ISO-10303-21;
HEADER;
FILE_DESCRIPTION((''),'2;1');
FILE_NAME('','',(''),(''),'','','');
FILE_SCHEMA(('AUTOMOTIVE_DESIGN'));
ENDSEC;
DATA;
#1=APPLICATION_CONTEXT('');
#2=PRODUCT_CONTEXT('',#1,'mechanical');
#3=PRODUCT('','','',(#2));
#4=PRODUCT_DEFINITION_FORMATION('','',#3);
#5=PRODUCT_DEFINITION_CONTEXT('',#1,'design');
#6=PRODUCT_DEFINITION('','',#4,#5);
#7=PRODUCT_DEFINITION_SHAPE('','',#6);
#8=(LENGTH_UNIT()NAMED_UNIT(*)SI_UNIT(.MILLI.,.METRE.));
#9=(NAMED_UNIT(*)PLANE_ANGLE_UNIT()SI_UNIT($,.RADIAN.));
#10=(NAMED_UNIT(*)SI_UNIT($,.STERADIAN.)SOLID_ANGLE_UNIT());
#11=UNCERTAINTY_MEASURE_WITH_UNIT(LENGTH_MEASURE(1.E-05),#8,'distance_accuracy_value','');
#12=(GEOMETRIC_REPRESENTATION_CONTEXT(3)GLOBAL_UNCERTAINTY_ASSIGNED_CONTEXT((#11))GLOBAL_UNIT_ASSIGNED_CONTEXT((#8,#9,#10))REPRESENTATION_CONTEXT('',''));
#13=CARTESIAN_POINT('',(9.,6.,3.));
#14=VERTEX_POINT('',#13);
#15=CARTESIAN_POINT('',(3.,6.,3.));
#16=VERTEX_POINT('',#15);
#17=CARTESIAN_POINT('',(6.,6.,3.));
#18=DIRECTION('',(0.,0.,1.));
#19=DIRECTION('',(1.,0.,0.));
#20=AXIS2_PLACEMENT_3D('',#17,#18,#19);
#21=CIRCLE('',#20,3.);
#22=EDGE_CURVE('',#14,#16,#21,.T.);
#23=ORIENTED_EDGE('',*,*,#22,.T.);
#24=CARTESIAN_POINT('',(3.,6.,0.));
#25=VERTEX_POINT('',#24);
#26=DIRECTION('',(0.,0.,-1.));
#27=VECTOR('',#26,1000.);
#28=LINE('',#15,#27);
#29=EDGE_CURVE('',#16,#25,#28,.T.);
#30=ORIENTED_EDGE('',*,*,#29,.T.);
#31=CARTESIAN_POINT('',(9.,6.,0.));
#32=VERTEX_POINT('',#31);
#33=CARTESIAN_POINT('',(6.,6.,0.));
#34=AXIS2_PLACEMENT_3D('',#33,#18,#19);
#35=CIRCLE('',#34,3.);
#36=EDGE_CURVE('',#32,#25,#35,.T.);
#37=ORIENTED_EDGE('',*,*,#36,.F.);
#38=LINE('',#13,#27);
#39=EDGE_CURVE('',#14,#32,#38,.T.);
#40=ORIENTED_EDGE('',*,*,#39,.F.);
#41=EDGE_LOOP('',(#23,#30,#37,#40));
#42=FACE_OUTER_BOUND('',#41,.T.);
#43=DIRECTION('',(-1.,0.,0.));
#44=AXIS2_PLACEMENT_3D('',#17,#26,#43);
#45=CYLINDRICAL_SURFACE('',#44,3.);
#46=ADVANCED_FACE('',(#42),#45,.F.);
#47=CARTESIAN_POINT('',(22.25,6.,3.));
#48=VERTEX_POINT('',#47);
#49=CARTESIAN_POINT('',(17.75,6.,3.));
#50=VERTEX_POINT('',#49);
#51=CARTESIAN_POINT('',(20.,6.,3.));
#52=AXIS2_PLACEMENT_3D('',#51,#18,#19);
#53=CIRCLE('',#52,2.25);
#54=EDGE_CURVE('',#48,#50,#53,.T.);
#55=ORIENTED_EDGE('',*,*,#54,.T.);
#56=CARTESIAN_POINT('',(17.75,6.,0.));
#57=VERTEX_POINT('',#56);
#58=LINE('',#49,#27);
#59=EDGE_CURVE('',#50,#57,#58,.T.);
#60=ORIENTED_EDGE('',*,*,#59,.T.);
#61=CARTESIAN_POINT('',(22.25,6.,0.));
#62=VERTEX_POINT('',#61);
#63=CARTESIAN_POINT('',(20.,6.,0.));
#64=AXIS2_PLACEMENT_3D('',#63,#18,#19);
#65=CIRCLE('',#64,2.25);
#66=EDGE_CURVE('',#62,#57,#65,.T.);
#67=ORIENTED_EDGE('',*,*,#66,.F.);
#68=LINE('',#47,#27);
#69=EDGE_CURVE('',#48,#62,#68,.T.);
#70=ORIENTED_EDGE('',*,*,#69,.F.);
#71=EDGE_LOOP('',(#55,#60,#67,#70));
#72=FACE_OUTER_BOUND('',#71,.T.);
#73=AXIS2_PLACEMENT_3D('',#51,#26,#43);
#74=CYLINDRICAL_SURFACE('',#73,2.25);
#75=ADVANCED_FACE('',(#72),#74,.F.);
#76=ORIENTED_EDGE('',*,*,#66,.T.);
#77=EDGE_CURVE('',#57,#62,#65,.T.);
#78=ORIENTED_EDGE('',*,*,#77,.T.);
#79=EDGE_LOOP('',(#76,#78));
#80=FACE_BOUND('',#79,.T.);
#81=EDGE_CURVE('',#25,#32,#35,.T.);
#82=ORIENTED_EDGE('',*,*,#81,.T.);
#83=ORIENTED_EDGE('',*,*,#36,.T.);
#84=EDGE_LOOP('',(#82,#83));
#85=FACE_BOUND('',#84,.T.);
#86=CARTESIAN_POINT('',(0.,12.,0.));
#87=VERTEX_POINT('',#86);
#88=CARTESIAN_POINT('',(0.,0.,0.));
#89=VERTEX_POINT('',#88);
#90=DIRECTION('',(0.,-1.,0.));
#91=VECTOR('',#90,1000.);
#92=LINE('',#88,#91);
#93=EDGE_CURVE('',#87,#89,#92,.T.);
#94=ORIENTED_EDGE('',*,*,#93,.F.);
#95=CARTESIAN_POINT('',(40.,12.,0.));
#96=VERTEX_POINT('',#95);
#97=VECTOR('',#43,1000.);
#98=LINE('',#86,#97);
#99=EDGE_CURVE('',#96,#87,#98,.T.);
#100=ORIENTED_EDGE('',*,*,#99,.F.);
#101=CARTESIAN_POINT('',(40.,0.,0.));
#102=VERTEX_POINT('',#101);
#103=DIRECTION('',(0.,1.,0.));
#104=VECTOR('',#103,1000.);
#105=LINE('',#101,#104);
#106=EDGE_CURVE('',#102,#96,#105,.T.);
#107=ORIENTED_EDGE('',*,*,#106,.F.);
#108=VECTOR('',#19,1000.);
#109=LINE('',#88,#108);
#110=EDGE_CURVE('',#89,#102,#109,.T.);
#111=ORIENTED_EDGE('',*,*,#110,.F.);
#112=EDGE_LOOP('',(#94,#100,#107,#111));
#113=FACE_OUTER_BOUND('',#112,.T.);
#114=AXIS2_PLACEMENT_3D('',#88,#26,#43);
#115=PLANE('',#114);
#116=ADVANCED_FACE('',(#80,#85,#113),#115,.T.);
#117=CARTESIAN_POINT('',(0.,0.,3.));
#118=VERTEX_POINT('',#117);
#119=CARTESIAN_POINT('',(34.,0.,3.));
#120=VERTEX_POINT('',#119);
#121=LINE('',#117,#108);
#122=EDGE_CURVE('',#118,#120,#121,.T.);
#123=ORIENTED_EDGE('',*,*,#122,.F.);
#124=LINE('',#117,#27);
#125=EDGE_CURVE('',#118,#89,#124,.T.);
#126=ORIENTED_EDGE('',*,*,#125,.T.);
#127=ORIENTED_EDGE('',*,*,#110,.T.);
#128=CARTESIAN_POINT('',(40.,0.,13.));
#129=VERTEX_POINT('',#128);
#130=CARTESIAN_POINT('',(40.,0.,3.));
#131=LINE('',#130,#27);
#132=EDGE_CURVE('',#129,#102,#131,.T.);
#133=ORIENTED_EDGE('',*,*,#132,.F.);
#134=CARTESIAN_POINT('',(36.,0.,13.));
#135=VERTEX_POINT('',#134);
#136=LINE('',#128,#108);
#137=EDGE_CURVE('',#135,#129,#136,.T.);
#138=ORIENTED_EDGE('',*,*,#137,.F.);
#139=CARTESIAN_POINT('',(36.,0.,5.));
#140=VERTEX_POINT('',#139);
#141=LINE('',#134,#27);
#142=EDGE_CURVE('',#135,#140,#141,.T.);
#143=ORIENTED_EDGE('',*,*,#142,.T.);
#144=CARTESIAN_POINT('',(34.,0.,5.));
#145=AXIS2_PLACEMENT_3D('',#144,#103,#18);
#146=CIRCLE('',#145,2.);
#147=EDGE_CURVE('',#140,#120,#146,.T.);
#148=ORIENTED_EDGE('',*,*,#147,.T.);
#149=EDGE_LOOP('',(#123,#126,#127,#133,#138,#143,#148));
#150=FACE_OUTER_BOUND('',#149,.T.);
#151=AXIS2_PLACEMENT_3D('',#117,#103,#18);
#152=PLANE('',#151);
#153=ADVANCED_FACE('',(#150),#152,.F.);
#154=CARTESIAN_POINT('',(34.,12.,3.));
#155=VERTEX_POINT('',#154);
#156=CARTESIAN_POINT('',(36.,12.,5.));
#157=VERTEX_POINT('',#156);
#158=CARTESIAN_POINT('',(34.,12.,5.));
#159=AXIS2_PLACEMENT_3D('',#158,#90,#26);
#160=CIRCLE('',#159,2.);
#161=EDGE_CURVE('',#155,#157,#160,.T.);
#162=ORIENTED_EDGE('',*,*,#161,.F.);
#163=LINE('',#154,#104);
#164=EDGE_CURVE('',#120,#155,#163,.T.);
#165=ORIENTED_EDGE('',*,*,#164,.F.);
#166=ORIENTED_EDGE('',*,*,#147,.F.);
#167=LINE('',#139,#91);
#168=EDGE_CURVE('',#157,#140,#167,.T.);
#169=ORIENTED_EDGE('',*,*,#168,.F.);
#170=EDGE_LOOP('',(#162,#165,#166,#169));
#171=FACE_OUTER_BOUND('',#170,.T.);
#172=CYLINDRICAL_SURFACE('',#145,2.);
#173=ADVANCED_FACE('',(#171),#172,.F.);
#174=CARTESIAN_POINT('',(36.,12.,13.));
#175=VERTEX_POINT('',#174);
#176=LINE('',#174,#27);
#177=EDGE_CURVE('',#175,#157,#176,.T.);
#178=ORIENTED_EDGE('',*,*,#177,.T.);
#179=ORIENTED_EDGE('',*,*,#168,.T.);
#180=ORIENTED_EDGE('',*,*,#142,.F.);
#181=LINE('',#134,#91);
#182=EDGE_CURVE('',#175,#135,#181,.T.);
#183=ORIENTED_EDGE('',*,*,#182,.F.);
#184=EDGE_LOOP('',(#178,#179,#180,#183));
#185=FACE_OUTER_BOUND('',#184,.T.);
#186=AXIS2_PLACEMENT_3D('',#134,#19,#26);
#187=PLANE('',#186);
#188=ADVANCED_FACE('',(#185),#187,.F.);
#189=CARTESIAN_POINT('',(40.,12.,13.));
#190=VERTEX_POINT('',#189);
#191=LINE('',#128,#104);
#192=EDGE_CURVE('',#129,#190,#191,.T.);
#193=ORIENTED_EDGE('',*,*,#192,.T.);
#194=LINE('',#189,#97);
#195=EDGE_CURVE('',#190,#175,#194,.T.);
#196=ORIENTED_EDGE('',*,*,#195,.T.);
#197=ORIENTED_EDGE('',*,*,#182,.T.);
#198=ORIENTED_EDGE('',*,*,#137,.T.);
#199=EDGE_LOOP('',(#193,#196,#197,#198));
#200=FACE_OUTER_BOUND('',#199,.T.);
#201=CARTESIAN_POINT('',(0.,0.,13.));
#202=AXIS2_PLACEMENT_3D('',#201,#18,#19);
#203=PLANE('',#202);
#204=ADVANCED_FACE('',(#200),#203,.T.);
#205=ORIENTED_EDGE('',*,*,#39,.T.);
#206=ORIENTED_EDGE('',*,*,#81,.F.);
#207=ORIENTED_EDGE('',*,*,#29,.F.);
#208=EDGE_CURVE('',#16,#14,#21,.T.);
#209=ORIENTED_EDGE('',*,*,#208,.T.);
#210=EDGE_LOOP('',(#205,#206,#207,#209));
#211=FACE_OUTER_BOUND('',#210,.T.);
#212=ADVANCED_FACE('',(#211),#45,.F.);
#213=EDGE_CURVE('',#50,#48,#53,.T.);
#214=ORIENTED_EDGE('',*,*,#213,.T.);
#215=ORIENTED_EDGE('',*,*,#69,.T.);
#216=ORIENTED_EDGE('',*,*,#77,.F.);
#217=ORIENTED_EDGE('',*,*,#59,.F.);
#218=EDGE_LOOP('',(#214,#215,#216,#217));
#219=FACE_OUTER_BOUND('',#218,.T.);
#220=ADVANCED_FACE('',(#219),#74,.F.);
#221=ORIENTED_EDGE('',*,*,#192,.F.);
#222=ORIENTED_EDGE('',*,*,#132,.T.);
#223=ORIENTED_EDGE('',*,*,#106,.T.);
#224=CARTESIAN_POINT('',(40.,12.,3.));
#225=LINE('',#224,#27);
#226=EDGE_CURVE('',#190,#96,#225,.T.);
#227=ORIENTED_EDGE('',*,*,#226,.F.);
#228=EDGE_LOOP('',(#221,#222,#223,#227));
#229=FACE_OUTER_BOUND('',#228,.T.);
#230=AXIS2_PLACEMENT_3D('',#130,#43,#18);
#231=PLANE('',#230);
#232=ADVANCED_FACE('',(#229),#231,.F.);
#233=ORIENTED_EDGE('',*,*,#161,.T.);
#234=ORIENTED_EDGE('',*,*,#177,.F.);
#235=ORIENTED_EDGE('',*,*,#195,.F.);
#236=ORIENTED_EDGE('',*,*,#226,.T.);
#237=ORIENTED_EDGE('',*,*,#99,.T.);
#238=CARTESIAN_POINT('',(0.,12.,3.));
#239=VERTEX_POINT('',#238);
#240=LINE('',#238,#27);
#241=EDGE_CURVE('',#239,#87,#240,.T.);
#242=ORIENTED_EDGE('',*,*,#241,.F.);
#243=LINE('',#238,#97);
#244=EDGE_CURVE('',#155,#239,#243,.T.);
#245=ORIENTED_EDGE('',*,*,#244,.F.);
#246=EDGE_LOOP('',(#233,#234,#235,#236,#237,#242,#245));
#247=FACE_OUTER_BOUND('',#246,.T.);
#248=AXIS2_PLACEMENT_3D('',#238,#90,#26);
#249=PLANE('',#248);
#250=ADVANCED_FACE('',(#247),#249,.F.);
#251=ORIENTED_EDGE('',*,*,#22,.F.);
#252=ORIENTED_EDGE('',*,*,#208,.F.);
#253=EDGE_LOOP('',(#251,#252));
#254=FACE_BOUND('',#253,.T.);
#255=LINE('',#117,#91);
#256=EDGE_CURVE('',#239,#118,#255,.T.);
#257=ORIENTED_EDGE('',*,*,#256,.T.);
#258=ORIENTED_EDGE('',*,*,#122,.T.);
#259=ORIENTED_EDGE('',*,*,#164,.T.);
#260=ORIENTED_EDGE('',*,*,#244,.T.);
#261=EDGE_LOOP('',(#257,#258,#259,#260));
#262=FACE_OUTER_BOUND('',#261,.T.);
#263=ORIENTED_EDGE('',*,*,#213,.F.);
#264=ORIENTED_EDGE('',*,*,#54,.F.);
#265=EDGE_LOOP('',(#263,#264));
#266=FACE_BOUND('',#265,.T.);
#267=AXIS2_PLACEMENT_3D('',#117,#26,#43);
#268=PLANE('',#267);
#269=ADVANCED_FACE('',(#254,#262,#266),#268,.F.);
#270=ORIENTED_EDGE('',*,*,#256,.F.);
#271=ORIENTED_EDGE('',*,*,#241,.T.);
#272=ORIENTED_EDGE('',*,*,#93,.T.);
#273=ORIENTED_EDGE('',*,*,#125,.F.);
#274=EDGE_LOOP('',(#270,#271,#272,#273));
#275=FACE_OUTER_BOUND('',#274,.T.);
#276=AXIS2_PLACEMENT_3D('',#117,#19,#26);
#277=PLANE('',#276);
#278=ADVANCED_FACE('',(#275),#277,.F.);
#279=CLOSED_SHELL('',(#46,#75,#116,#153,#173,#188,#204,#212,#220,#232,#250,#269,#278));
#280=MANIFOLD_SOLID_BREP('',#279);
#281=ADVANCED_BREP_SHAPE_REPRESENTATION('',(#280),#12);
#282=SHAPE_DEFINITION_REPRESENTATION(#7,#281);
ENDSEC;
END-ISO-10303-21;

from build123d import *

# Parameters (mm, degrees)
SKETCH1_W           = 40
SKETCH1_H           = 12
SKETCH1_R           = 2.25
SKETCH1_R_2         = 3
BOSS_EXTRUDE1_DEPTH = 3
SKETCH2_W           = 4
SKETCH2_H           = 12
BOSS_EXTRUDE2_DEPTH = 10
FILLET1_R           = 2


with BuildPart() as part:
    # Sketch1 → Boss-Extrude1 (new body)
    with BuildSketch(Plane.XY):
        with Locations((20, 6)):
            Rectangle(SKETCH1_W, SKETCH1_H)
        with Locations((20, 6)):
            Circle(SKETCH1_R, mode=Mode.SUBTRACT)
        with Locations((6, 6)):
            Circle(SKETCH1_R_2, mode=Mode.SUBTRACT)
    extrude(amount=BOSS_EXTRUDE1_DEPTH)

    # Sketch2 → Boss-Extrude2 (add)
    with BuildSketch(Plane.XY.offset(3)):
        with Locations((38, 6)):
            Rectangle(SKETCH2_W, SKETCH2_H)
    extrude(amount=BOSS_EXTRUDE2_DEPTH)

    # Fillet1
    fillet1_edges = [part.edges().sort_by_distance(p)[0] for p in [
        (36, 6, 3),
    ]]
    fillet(fillet1_edges, radius=FILLET1_R)


solid = part.part
